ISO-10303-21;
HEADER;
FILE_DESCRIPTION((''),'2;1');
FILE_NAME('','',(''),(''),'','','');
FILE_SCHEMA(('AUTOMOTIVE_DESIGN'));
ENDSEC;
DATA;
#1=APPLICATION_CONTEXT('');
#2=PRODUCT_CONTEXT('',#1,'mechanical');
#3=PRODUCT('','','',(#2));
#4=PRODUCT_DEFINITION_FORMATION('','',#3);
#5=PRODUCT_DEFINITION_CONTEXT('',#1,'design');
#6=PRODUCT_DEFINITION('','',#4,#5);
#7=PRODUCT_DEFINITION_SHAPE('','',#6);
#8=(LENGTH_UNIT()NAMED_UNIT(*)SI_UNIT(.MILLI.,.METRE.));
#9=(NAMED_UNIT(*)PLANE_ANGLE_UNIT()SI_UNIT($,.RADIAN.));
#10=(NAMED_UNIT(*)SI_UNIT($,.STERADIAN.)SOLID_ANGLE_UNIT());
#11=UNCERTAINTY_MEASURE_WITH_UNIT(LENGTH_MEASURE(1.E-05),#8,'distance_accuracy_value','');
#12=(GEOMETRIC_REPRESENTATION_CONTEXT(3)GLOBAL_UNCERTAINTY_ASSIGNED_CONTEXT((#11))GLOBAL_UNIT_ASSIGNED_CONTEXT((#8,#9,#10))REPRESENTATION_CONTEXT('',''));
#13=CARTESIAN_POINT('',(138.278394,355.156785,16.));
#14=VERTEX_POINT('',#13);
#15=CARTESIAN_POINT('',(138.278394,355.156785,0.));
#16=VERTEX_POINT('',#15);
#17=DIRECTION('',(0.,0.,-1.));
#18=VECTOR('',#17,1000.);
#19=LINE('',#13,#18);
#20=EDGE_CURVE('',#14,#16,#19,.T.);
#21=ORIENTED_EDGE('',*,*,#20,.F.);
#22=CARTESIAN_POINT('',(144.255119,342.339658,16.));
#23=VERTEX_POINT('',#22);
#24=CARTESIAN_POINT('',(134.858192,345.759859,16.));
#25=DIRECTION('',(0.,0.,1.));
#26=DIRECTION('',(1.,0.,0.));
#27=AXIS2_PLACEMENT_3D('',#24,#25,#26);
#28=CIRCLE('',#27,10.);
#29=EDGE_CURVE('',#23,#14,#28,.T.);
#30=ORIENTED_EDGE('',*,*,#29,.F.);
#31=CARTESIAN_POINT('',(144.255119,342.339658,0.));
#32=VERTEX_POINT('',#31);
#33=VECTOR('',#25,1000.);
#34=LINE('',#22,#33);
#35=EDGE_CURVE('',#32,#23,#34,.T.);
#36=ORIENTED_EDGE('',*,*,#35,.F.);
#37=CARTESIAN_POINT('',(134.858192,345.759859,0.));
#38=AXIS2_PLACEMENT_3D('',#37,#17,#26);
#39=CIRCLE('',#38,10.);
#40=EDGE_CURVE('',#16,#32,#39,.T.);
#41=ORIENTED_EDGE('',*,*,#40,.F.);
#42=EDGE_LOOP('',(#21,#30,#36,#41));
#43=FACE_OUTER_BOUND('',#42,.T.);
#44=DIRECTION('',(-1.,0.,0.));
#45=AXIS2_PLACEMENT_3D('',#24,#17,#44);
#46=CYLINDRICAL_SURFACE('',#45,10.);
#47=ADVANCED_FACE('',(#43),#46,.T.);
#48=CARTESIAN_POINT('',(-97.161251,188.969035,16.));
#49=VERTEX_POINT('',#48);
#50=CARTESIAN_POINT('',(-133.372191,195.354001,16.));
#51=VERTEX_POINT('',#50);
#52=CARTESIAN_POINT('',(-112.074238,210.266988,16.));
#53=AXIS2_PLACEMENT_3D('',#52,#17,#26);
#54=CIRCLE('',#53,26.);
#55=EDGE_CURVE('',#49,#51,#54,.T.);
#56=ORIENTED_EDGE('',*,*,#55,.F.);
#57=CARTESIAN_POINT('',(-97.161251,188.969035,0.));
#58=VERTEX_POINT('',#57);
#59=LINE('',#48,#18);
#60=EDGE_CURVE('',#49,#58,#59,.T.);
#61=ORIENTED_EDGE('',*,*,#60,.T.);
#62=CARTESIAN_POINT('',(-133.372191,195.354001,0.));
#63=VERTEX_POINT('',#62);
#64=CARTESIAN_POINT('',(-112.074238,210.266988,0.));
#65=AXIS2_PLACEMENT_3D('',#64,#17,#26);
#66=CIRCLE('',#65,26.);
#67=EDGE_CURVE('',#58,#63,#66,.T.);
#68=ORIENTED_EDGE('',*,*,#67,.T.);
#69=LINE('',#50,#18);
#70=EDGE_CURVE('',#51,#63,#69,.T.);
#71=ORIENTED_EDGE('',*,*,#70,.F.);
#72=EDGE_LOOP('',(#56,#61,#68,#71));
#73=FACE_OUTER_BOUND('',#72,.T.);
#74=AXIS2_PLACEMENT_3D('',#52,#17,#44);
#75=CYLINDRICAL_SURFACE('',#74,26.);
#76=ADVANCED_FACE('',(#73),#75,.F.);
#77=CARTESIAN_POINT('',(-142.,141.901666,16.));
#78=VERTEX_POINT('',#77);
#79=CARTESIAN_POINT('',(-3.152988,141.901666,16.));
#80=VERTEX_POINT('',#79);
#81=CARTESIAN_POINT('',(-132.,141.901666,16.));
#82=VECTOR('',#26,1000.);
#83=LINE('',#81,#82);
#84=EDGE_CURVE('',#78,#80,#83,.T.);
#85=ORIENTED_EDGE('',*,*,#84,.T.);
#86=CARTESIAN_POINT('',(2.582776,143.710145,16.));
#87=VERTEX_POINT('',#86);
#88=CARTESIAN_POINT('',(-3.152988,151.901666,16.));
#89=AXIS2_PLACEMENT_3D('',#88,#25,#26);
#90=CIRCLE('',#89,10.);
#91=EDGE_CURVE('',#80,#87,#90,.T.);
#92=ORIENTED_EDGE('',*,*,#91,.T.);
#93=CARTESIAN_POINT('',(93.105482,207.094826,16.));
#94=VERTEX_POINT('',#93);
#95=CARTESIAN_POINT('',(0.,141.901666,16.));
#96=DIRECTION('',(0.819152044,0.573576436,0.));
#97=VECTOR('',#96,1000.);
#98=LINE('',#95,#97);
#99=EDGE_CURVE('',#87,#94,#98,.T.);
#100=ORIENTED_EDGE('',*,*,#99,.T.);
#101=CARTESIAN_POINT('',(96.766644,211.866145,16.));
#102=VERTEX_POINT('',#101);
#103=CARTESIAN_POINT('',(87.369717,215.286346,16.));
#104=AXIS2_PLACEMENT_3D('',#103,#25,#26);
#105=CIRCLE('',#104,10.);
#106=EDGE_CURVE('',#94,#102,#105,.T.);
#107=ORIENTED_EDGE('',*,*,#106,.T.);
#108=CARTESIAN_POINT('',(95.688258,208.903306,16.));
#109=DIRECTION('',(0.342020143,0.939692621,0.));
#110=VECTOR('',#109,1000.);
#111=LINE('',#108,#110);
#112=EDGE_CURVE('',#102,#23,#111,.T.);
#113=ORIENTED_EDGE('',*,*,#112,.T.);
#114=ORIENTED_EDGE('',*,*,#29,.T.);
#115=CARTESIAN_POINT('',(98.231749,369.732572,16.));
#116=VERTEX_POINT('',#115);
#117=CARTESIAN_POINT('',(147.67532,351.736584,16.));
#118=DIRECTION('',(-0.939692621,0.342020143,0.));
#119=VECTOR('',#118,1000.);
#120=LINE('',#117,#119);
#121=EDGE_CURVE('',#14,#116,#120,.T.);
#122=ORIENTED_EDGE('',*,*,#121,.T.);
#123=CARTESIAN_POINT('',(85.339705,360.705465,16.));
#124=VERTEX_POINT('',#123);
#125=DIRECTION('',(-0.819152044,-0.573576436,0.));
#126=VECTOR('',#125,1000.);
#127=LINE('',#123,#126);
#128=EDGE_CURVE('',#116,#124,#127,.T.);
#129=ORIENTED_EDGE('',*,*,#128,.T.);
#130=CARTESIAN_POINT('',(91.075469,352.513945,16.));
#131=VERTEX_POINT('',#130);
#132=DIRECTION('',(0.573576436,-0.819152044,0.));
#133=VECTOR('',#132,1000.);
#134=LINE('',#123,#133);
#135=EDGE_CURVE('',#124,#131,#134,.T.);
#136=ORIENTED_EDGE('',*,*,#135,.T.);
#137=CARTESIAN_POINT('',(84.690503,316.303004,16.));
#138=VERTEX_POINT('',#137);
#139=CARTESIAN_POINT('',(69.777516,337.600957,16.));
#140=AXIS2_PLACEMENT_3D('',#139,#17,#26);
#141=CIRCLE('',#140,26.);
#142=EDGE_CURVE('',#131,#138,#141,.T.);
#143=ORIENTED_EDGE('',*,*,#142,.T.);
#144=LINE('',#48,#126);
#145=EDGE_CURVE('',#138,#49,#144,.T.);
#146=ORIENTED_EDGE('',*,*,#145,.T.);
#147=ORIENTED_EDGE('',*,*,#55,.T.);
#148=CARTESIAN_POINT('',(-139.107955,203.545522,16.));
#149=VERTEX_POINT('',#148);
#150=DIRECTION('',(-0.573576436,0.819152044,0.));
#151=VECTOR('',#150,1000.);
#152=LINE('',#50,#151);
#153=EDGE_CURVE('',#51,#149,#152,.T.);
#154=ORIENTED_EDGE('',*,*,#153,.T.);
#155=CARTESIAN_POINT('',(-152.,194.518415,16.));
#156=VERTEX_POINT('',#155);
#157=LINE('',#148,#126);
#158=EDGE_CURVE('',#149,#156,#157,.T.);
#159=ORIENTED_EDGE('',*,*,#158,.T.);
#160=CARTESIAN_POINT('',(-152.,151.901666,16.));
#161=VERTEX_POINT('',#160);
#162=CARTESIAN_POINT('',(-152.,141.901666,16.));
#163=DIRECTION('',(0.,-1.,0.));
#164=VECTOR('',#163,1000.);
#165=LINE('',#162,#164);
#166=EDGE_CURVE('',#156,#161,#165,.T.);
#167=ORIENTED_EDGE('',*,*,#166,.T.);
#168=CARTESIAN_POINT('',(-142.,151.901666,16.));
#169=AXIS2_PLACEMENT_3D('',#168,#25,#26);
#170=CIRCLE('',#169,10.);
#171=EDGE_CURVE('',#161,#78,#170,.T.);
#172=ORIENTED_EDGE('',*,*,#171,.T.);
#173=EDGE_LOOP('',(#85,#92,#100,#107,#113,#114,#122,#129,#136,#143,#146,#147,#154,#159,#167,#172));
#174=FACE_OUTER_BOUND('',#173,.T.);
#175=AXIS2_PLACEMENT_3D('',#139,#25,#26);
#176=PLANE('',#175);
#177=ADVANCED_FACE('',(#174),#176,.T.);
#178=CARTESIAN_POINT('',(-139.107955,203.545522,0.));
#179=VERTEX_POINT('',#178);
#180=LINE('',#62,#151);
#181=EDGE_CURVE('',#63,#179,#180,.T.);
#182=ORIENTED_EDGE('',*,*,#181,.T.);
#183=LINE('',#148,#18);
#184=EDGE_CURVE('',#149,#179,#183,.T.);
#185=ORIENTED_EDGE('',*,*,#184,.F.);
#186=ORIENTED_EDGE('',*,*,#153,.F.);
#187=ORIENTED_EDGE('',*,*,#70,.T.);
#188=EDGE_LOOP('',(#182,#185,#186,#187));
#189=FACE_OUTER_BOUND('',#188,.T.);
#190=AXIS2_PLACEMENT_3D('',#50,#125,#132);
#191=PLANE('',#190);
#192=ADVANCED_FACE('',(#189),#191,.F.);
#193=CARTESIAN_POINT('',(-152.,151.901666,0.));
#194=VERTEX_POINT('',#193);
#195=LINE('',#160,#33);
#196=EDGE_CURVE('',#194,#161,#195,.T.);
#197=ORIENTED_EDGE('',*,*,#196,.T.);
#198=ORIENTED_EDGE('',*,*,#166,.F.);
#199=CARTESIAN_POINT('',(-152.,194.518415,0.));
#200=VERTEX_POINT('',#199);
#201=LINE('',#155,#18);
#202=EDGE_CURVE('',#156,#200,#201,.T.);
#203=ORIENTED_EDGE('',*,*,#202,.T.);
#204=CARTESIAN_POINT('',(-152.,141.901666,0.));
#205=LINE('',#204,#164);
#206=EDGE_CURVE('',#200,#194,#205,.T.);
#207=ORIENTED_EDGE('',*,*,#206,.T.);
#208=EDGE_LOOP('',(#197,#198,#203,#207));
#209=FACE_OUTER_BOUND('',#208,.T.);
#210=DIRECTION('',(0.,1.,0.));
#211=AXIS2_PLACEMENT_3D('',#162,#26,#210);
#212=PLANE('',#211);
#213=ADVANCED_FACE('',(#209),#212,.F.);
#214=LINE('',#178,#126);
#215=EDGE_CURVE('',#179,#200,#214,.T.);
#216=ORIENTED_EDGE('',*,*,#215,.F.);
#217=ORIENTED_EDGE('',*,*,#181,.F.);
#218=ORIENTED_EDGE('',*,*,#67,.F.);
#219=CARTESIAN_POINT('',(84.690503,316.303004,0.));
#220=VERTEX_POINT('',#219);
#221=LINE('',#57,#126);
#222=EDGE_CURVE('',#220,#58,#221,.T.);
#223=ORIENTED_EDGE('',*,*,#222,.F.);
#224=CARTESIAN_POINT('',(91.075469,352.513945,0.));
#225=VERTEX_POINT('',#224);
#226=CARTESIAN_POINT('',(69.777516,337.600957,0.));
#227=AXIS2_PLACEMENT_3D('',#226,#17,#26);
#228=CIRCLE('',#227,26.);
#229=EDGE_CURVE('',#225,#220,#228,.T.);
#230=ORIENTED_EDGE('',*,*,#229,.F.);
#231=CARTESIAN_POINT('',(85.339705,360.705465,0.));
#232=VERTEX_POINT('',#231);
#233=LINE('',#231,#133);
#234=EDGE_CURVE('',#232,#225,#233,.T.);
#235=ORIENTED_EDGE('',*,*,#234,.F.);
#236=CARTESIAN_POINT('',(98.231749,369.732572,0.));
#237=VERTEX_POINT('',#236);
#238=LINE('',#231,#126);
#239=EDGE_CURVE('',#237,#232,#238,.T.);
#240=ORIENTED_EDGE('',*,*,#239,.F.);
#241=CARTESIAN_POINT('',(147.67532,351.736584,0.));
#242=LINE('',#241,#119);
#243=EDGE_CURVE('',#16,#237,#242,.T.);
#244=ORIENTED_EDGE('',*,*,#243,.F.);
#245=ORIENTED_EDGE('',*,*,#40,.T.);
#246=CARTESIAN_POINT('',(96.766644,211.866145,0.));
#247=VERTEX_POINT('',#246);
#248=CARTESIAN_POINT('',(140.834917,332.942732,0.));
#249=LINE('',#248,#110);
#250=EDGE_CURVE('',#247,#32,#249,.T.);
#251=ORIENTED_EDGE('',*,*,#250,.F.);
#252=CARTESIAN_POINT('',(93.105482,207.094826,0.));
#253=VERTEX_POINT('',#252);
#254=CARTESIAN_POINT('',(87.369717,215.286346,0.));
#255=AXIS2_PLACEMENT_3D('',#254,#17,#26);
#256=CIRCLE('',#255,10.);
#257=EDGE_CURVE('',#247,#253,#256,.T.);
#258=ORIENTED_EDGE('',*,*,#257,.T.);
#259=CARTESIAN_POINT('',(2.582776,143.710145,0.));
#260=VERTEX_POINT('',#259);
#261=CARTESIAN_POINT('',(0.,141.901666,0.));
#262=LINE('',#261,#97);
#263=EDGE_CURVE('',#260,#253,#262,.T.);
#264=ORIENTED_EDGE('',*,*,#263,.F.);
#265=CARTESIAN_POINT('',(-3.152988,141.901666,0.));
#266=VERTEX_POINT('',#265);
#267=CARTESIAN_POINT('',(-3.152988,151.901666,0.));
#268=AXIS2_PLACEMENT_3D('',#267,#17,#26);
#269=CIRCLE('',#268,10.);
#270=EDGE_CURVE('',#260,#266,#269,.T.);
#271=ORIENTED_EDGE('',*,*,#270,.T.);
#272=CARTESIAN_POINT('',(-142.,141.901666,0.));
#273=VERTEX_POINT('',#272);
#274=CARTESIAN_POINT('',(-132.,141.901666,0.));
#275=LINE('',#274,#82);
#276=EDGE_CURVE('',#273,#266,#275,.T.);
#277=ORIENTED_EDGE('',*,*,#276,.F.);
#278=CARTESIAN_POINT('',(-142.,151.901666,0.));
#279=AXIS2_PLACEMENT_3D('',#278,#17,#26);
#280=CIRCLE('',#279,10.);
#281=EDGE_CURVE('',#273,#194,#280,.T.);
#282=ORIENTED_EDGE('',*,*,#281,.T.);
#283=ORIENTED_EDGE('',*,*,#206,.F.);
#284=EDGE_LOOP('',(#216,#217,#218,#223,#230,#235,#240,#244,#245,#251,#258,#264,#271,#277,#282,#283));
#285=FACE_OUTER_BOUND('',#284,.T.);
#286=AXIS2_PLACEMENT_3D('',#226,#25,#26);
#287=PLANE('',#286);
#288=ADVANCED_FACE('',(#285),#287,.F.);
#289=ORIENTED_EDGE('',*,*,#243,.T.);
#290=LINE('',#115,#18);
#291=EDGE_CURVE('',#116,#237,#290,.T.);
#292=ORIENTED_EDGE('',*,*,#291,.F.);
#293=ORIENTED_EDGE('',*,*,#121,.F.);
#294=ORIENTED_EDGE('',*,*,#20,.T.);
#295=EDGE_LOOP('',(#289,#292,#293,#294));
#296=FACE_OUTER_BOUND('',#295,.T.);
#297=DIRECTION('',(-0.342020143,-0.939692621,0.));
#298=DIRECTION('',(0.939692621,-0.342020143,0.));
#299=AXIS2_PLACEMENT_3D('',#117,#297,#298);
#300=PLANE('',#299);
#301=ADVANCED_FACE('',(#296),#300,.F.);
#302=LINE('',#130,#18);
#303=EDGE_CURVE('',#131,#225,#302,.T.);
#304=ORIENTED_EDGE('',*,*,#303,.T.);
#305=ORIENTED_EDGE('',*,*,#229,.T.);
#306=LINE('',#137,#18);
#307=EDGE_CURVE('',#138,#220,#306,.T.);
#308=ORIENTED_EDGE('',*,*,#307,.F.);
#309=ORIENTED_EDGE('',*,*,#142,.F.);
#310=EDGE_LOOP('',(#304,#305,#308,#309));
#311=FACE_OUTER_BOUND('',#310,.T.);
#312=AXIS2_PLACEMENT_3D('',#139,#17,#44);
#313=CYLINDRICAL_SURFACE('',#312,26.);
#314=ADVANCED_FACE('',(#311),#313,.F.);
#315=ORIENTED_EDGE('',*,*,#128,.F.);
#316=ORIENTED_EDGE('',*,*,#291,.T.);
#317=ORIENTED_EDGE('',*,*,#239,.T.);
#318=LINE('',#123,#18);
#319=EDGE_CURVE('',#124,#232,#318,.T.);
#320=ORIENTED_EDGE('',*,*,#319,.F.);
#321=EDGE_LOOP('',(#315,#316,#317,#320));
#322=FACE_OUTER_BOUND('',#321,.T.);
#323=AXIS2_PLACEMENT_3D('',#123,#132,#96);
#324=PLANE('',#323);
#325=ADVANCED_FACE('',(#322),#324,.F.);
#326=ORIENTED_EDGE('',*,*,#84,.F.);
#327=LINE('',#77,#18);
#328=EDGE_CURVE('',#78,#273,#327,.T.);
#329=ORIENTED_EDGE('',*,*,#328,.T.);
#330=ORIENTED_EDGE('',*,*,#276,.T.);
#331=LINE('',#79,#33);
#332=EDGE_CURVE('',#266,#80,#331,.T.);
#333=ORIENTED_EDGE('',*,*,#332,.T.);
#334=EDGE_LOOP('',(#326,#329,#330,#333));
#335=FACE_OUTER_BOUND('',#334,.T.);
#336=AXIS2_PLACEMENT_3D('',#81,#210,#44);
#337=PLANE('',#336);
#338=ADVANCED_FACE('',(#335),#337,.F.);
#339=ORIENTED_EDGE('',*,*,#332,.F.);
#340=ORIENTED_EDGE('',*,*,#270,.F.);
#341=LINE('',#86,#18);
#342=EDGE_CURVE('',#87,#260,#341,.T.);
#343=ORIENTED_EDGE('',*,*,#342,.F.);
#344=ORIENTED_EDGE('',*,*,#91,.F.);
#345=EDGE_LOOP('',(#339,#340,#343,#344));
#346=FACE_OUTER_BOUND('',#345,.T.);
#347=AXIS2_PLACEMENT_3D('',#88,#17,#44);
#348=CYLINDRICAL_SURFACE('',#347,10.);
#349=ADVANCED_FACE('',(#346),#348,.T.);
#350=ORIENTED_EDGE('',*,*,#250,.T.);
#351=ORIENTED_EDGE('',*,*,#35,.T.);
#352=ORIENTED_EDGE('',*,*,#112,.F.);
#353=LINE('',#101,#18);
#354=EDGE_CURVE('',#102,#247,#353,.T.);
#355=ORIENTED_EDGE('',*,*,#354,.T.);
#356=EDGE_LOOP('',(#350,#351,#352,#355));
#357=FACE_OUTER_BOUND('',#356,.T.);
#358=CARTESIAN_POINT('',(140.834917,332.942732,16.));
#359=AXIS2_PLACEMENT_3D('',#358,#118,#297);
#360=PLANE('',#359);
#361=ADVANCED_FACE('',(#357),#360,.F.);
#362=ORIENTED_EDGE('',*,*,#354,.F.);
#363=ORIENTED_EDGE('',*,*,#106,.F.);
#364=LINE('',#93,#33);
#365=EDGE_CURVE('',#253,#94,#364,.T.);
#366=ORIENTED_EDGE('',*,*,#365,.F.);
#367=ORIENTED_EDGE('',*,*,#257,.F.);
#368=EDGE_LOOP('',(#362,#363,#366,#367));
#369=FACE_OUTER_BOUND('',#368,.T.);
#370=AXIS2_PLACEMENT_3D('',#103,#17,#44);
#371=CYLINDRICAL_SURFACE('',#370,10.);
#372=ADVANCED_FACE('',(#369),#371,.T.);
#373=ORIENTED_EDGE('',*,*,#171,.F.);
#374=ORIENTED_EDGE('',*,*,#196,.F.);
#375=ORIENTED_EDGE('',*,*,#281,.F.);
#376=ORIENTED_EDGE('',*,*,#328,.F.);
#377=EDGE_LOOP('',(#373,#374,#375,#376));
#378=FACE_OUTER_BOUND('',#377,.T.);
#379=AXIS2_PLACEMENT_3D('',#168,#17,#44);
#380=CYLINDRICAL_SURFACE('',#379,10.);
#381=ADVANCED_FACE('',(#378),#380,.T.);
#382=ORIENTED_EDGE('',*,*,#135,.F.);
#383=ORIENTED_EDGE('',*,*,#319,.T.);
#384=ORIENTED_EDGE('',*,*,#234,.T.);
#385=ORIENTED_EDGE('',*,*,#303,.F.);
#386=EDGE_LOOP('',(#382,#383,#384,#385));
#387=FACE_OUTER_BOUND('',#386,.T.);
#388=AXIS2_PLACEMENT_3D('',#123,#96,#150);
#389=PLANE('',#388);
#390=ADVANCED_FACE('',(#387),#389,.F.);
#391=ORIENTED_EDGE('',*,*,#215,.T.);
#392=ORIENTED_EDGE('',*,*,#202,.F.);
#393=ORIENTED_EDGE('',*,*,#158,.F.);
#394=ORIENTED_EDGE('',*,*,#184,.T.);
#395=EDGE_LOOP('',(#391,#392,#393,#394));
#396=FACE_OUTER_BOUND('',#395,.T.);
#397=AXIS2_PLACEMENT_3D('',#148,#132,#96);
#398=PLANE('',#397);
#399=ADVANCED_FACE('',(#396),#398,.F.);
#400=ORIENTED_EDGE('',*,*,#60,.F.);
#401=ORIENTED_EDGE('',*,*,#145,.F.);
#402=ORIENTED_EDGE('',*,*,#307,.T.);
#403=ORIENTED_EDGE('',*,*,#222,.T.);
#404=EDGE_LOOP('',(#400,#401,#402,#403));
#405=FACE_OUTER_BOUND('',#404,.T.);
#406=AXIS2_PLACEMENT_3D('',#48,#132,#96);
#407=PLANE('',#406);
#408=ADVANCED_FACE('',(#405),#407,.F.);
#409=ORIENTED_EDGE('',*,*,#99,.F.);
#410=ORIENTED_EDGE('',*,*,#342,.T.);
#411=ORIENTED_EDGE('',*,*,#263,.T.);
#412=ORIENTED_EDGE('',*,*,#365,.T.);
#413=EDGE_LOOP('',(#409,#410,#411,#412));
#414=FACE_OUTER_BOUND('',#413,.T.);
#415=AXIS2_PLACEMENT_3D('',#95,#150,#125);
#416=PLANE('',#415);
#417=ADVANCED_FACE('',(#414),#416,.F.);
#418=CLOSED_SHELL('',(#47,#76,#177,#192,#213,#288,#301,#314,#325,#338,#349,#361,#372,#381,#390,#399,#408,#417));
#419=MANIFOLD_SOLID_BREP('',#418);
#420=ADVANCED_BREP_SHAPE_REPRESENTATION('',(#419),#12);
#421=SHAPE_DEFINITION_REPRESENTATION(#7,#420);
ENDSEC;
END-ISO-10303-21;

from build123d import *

# Parameters (mm, degrees)
EXTRUDE_1_DEPTH = 16
FILLET_1_R      = 10


with BuildPart() as part:
    # 草图1 → 凸台-拉伸1 (new body)
    with BuildSketch(Plane.XY):
        with BuildLine():
            Line((-132, 141.901665764), (-152, 141.901665764))
            Line((-152, 141.901665764), (-152, 194.51841477))
            Line((-152, 194.51841477), (-139.107955396, 203.545521584))
            Line((-139.107955396, 203.545521584), (-133.372191032, 195.354001142))
            ThreePointArc((-133.372191032, 195.354001142), (-116.5890905, 184.661986908), (-97.161250536, 188.969035335))
            Line((-97.161250536, 188.969035335), (84.690503297, 316.303004205))
            ThreePointArc((84.690503297, 316.303004205), (95.38251753, 333.086104737), (91.075469103, 352.513944702))
            Line((91.075469103, 352.513944702), (85.339704739, 360.705465145))
            Line((85.339704739, 360.705465145), (98.231749344, 369.732571959))
            Line((98.231749344, 369.732571959), (147.675320114, 351.736583923))
            Line((147.675320114, 351.736583923), (140.834917247, 332.942731507))
            Line((140.834917247, 332.942731507), (95.688258328, 208.903305564))
            Line((95.688258328, 208.903305564), (0, 141.901665764))
            Line((0, 141.901665764), (-132, 141.901665764))
        make_face()
    extrude(amount=EXTRUDE_1_DEPTH)

    # 圆角1
    fillet_1_edges = [part.edges().sort_by_distance(p)[0] for p in [
        (-152, 141.901665764, 8),
        (147.675320114, 351.736583923, 8),
        (95.688258328, 208.903305564, 8),
        (0, 141.901665764, 8),
    ]]
    fillet(fillet_1_edges, radius=FILLET_1_R)


solid = part.part
